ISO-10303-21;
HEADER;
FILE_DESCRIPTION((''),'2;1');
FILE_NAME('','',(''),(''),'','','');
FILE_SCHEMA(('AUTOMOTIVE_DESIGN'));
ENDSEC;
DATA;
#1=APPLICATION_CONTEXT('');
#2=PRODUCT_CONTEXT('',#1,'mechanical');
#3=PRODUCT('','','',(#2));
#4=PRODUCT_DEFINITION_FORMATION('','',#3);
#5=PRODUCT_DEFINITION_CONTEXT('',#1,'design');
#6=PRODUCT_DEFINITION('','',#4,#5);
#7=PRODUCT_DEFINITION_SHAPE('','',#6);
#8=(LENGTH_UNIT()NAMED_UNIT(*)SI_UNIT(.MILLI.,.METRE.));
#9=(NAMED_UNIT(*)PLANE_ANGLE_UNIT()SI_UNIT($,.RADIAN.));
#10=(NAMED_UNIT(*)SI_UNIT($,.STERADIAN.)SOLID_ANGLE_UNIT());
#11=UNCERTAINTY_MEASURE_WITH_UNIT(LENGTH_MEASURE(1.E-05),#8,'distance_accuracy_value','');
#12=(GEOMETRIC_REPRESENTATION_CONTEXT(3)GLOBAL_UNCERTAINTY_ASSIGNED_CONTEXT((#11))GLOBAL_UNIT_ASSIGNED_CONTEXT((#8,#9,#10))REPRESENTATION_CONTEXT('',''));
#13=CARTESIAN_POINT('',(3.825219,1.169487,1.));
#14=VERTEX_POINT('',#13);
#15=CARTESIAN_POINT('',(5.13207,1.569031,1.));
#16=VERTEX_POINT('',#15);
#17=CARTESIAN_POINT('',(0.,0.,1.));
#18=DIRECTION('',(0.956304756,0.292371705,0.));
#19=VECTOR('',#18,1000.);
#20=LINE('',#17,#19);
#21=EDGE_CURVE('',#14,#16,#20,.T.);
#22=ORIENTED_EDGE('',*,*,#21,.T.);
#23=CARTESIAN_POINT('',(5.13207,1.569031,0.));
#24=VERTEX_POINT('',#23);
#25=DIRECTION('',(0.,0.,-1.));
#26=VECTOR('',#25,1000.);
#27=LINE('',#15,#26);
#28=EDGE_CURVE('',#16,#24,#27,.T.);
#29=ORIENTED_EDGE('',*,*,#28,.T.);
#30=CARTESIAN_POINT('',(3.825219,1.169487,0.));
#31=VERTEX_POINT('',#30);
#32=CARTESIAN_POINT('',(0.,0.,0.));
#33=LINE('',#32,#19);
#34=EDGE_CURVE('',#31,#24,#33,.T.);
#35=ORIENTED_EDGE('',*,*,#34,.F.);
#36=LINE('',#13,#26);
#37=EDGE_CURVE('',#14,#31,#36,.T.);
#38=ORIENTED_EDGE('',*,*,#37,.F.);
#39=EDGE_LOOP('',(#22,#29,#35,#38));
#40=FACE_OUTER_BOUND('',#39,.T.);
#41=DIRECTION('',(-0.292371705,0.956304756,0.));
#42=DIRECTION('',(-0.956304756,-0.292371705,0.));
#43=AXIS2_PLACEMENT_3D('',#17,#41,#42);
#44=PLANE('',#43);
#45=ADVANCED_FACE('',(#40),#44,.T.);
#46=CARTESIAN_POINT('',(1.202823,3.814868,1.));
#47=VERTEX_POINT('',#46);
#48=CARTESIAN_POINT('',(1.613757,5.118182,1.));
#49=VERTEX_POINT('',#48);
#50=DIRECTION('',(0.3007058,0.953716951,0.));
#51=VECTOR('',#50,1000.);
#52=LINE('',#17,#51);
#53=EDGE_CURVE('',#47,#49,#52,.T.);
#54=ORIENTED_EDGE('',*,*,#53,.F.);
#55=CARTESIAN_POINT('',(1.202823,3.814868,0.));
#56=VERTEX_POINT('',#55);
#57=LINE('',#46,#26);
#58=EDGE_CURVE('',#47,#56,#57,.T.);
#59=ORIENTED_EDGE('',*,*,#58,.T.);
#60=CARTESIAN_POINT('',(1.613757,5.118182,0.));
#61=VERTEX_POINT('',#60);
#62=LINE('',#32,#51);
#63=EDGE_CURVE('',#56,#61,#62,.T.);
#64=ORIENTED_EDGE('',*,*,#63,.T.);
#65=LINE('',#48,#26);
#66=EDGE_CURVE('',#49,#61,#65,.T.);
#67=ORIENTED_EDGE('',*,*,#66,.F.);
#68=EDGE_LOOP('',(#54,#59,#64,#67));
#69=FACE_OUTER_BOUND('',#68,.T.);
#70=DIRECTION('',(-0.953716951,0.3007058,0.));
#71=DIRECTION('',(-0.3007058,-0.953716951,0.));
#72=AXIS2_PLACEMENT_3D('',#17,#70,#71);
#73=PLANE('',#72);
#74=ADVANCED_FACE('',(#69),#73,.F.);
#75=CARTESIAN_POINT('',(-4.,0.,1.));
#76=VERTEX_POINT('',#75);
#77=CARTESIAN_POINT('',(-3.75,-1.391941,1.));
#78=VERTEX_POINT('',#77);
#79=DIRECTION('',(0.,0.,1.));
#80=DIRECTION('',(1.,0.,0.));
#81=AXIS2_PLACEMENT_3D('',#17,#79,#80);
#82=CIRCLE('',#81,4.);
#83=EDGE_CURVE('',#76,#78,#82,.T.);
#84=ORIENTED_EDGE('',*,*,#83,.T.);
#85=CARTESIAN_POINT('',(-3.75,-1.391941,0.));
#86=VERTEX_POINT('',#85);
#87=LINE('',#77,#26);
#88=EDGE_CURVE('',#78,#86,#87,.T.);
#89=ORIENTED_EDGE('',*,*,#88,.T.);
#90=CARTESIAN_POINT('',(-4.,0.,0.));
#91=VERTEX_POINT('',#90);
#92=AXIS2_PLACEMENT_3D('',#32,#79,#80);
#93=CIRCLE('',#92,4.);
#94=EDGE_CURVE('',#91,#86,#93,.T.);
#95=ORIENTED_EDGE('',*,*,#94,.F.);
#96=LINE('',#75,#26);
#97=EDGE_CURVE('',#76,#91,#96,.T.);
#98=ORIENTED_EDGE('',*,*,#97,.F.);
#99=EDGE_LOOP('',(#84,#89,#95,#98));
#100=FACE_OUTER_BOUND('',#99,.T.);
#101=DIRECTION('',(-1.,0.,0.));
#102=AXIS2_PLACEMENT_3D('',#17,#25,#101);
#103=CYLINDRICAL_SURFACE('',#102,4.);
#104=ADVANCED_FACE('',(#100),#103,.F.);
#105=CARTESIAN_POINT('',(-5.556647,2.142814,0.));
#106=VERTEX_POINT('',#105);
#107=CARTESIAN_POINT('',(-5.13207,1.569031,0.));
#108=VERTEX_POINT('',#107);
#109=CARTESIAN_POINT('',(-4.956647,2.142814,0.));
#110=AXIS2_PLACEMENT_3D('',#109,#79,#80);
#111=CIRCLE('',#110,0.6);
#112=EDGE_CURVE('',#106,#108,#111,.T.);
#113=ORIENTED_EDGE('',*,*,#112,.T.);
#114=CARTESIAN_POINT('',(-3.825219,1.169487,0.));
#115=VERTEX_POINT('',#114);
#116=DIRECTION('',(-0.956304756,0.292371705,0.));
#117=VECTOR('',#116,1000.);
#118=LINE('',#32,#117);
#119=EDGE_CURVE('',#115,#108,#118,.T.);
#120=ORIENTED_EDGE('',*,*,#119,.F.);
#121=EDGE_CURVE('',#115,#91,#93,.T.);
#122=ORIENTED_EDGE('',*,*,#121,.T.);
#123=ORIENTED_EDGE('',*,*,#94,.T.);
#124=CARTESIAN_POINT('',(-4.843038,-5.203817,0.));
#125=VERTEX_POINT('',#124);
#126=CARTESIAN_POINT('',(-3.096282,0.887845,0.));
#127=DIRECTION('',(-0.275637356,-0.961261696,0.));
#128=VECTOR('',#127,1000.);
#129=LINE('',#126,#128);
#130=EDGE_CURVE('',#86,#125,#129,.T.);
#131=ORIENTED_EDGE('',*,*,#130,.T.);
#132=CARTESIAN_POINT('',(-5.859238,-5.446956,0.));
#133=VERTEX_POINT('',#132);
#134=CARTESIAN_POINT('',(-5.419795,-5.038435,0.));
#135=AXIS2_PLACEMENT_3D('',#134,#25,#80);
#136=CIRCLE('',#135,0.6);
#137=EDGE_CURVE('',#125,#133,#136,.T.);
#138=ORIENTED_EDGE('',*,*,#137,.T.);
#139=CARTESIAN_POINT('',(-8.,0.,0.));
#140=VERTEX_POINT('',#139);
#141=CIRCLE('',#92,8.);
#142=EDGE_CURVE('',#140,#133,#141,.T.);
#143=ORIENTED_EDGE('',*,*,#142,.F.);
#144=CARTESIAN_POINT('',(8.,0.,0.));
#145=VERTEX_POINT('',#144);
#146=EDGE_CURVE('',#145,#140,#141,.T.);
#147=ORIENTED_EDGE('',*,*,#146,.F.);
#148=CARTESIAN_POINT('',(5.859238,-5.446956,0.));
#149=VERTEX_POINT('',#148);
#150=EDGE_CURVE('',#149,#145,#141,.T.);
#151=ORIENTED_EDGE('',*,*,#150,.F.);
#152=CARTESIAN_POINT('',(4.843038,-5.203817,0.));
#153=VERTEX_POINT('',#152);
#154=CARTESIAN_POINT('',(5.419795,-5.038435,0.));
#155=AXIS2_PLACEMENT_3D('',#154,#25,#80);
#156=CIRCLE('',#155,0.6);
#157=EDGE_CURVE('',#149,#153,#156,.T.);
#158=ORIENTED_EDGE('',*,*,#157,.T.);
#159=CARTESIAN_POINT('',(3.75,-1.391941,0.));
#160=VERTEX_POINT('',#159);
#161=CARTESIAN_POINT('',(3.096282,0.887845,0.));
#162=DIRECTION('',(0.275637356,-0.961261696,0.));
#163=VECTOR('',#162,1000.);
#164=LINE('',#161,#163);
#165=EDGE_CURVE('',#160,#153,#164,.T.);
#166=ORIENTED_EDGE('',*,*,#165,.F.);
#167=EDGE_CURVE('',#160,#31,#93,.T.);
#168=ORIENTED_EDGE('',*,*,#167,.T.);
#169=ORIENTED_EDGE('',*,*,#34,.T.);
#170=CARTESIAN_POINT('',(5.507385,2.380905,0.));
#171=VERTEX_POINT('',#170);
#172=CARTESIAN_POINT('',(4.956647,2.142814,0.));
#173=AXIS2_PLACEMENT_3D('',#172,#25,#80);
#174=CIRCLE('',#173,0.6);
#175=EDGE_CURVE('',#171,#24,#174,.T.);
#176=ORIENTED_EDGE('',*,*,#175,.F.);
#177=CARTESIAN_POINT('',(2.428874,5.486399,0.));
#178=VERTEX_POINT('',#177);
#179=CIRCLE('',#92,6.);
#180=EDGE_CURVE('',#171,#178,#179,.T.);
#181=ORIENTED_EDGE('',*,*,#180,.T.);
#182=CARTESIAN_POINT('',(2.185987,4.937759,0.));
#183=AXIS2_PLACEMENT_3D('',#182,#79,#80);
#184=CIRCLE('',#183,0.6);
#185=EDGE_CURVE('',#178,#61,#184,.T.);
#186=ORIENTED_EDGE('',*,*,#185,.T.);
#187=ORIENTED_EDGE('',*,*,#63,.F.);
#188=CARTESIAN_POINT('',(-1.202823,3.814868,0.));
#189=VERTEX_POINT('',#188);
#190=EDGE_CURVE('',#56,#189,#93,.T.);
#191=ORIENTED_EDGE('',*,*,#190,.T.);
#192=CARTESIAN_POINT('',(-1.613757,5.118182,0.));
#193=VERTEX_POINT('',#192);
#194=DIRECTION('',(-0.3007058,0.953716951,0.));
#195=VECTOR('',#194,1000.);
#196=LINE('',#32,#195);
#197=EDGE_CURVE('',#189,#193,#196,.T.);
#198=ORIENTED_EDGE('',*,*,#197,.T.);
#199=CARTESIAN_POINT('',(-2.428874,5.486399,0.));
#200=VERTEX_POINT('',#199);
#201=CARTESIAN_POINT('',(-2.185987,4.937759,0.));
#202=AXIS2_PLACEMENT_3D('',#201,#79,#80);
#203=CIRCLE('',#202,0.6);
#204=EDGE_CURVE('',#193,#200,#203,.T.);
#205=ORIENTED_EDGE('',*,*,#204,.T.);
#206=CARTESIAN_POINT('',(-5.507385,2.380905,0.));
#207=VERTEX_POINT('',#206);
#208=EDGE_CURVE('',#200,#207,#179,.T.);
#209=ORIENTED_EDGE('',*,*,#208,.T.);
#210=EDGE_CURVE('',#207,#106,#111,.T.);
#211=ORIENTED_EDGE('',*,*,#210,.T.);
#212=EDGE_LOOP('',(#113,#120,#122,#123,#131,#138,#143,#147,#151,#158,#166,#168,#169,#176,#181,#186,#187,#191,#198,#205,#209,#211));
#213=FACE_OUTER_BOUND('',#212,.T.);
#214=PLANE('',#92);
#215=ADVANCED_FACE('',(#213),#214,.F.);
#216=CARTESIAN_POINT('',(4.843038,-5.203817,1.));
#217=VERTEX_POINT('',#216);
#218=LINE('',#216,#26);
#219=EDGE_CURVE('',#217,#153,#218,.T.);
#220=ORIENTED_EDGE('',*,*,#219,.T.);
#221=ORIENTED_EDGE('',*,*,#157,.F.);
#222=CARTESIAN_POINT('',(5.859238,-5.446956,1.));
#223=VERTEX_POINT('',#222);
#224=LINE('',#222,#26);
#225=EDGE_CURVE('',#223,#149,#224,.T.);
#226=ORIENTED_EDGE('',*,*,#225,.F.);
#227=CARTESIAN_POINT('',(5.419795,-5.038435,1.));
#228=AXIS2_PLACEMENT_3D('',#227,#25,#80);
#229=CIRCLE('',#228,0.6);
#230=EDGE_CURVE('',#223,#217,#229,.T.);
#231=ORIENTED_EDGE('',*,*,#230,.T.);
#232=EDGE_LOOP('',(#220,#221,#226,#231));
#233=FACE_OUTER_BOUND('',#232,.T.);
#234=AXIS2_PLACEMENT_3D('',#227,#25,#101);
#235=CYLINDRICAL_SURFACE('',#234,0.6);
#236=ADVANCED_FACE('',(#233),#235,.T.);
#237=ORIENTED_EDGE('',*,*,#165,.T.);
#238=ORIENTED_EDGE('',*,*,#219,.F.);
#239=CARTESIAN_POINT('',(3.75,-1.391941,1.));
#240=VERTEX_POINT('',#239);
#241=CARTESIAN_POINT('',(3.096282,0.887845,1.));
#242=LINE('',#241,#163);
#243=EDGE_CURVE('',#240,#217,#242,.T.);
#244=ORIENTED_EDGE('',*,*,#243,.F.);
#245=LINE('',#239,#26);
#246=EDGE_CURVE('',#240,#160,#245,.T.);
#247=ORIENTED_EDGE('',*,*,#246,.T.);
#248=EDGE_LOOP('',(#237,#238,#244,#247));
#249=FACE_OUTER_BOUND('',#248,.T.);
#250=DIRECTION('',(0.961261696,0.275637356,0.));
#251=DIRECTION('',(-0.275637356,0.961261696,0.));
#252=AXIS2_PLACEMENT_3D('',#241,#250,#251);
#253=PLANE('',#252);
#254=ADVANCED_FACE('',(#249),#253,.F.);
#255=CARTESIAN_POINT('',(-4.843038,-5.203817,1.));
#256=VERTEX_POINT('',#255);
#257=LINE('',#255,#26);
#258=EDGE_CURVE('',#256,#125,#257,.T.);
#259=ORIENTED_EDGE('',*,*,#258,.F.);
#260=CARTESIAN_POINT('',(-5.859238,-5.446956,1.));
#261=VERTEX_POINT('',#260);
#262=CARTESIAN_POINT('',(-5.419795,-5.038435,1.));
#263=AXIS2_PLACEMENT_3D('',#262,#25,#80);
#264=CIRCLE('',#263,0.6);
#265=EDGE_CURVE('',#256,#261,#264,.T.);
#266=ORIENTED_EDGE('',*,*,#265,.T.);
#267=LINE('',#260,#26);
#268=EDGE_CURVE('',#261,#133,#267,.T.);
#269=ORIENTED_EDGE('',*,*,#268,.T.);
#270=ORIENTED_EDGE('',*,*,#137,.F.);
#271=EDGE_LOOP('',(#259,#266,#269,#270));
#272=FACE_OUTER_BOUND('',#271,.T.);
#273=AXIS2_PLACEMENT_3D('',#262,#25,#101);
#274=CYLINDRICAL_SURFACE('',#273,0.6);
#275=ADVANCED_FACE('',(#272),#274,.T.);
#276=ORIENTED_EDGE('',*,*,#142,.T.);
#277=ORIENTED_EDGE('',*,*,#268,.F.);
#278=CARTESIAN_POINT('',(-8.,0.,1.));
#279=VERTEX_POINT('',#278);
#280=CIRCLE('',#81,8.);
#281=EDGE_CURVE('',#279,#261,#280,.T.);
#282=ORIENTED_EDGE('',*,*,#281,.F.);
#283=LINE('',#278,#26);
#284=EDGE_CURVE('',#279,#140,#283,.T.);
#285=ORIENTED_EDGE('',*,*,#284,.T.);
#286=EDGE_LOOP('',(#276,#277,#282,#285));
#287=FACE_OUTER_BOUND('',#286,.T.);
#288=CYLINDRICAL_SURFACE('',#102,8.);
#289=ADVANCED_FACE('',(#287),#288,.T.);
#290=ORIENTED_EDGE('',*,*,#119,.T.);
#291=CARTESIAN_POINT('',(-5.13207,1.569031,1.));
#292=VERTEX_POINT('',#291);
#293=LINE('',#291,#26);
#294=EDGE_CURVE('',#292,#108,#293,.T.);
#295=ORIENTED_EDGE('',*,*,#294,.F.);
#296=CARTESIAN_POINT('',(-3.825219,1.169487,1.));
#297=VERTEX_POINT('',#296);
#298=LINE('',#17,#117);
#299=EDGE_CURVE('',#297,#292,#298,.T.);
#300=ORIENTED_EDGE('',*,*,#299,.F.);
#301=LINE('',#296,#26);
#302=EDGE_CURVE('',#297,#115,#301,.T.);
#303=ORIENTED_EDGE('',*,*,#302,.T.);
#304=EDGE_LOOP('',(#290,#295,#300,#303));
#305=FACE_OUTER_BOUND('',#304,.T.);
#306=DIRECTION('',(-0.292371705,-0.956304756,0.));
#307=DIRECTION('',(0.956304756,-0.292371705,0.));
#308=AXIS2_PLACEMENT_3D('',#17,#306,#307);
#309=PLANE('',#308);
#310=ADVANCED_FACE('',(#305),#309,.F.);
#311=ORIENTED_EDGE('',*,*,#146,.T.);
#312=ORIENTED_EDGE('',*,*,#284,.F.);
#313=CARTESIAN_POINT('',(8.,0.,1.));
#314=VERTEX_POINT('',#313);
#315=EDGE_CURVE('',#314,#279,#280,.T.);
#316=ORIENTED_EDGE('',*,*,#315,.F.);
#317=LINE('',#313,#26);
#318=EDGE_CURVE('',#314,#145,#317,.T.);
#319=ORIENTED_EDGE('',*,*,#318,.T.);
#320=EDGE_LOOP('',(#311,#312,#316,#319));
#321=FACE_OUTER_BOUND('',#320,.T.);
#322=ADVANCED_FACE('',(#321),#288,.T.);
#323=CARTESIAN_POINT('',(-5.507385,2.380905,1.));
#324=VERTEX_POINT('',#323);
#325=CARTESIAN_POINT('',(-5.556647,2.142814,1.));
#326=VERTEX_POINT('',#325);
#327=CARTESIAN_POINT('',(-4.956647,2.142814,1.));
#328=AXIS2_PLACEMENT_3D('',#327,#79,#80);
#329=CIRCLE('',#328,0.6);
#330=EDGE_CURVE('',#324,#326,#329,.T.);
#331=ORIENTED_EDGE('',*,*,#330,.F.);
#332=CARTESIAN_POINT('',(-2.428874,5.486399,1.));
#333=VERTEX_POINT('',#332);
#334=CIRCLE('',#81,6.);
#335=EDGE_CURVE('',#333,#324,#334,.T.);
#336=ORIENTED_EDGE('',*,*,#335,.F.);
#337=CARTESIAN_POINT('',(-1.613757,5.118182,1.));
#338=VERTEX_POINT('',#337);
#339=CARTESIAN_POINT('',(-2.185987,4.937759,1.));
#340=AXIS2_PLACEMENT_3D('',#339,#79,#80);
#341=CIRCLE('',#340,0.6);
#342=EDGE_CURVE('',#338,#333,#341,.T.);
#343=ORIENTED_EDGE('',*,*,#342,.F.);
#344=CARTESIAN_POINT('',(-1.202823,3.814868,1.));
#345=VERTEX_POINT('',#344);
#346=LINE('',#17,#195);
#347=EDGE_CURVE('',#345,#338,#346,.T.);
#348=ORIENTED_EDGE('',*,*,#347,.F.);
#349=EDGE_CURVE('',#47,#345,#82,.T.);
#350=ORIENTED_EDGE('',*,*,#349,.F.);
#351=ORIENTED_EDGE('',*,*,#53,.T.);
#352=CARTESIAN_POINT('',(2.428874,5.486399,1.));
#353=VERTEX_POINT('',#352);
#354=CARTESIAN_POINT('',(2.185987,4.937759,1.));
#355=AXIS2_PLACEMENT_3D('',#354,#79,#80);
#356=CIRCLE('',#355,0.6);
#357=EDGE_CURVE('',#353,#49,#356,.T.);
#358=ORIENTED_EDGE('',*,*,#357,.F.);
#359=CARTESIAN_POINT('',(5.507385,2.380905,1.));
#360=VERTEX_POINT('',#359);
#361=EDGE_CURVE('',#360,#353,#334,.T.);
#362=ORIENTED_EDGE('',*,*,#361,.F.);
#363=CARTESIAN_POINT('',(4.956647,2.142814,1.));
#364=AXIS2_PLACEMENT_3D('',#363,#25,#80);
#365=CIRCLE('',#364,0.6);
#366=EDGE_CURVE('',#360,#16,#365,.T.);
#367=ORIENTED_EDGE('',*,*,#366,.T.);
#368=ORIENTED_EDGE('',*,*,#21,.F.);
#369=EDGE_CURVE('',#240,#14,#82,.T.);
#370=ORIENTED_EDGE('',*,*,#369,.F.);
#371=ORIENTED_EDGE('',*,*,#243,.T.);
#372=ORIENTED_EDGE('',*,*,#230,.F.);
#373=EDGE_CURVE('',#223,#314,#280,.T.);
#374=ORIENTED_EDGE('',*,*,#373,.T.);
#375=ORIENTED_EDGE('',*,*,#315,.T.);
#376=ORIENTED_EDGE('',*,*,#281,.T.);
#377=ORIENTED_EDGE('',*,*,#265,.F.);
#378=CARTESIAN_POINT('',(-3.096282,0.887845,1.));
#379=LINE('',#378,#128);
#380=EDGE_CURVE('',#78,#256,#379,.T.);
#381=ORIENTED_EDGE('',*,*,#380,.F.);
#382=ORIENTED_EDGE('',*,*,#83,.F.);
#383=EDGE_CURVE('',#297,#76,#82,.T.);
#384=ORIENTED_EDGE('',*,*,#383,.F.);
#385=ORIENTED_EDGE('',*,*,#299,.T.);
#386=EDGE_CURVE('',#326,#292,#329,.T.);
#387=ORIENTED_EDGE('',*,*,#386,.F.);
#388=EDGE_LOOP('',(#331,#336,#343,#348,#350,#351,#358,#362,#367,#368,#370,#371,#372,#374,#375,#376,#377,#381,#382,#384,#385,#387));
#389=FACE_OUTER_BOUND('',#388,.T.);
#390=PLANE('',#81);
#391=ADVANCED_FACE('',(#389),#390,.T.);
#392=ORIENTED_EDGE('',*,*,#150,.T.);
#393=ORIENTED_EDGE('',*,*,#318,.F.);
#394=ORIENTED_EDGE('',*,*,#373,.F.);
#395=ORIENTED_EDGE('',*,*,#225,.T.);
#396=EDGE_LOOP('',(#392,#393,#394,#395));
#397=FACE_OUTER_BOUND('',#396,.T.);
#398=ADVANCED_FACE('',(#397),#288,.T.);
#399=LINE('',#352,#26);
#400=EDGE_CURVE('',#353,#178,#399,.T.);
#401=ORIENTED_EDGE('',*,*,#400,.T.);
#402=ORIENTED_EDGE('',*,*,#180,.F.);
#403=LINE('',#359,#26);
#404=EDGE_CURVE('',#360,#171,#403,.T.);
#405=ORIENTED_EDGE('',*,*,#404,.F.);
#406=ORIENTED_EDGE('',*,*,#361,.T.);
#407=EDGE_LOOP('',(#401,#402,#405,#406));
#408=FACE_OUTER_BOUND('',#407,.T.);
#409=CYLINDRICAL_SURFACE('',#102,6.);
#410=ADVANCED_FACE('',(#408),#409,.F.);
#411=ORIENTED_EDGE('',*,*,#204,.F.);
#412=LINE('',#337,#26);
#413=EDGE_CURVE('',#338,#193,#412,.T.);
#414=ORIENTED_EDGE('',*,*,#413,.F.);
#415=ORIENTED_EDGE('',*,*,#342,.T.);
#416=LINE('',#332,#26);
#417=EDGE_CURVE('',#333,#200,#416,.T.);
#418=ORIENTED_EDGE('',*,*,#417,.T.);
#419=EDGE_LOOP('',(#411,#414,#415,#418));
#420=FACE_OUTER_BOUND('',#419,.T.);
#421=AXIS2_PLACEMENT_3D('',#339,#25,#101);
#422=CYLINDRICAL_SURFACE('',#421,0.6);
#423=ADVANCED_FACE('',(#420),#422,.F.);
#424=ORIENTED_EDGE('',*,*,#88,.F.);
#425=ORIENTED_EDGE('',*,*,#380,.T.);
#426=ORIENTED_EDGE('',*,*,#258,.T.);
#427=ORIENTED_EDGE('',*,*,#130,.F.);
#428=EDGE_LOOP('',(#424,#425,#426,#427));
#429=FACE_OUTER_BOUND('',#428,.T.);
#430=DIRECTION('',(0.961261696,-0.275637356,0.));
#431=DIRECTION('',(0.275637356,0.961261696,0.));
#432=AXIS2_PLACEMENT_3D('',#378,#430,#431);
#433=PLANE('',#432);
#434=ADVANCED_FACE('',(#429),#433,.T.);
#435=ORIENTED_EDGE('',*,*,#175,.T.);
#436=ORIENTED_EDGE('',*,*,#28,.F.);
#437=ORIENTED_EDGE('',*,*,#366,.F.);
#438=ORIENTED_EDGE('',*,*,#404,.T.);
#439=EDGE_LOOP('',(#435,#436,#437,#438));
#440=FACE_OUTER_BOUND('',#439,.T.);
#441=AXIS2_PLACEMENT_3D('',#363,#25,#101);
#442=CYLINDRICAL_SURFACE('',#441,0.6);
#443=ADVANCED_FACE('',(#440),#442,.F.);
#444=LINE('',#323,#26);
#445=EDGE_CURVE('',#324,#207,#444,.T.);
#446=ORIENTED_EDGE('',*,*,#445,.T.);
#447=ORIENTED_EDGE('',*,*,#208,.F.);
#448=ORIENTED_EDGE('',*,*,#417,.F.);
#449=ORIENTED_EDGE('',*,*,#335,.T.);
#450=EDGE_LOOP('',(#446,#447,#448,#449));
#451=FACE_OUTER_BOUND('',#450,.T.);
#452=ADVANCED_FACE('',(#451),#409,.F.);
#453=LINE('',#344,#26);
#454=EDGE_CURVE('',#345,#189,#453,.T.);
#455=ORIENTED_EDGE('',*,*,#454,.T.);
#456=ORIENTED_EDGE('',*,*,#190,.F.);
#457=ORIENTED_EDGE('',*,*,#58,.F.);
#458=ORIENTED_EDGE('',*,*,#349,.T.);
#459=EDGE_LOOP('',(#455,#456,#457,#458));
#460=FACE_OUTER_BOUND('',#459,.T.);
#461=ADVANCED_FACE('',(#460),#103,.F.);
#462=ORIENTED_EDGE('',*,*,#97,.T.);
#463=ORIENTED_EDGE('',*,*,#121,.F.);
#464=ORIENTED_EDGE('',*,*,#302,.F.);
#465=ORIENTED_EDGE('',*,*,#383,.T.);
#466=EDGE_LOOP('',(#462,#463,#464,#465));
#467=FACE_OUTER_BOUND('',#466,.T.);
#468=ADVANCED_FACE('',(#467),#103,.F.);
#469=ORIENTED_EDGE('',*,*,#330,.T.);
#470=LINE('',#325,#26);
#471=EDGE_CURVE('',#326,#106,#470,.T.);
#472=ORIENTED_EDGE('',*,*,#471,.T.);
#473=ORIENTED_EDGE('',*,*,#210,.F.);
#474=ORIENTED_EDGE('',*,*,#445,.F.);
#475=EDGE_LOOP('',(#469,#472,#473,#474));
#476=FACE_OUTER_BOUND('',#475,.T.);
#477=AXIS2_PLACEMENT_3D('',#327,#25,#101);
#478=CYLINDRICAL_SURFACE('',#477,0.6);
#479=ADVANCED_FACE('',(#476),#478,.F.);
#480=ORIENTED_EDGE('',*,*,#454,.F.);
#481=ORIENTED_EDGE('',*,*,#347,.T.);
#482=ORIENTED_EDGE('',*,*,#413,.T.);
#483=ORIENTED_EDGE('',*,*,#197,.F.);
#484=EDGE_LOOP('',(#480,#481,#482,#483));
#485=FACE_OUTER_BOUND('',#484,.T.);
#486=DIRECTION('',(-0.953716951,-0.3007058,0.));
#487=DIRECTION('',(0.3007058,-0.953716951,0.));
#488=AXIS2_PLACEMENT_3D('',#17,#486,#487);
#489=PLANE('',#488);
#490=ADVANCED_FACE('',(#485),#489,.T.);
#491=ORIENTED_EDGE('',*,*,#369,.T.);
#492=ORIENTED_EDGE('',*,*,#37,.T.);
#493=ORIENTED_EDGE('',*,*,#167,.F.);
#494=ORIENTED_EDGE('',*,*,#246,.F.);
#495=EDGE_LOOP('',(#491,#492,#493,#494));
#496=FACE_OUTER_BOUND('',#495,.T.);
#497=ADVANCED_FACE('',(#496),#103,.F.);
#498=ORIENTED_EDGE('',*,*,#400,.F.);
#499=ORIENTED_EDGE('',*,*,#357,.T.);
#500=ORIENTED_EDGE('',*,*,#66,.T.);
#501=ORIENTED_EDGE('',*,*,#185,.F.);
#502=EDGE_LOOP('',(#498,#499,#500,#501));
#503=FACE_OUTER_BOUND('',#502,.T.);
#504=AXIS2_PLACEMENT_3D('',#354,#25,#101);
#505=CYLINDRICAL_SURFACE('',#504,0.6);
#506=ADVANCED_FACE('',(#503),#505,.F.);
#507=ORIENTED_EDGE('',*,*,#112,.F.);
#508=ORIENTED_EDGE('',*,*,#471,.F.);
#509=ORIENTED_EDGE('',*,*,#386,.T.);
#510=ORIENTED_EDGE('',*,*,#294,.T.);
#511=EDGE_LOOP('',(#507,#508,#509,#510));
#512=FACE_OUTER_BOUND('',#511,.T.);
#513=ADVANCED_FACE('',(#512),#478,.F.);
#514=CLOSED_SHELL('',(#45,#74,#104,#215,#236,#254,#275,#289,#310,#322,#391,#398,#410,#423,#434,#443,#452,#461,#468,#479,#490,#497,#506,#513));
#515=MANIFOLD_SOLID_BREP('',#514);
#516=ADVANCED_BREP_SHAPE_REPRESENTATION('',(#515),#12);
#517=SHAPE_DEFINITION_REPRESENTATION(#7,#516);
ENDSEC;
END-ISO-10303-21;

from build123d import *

# Parameters (mm, degrees)
EXTRUDE1_DEPTH = 1


with BuildPart() as part:
    # Sketch1 → Extrude1 (new body)
    with BuildSketch(Plane.XY):
        with BuildLine():
            Line((3.75, -1.391941091), (4.843037844, -5.203817057))
            ThreePointArc((4.843037844, -5.203817057), (5.280177605, -5.621964438), (5.859237689, -5.446956371))
            ThreePointArc((5.859237689, -5.446956371), (0, 8), (-5.859237689, -5.446956371))
            ThreePointArc((-5.859237689, -5.446956371), (-5.280177605, -5.621964438), (-4.843037844, -5.203817057))
            Line((-4.843037844, -5.203817057), (-3.75, -1.391941091))
            ThreePointArc((-3.75, -1.391941091), (-3.998276385, -0.11741359), (-3.825219024, 1.169486819))
            Line((-3.825219024, 1.169486819), (-5.13206986, 1.569031215))
            ThreePointArc((-5.13206986, 1.569031215), (-5.501268007, 1.891044768), (-5.507385374, 2.380904521))
            ThreePointArc((-5.507385374, 2.380904521), (-4.261112254, 4.224088347), (-2.428874258, 5.486398622))
            ThreePointArc((-2.428874258, 5.486398622), (-1.938979773, 5.484556266), (-1.613756661, 5.11818224))
            Line((-1.613756661, 5.11818224), (-1.202823198, 3.814867803))
            ThreePointArc((-1.202823198, 3.814867803), (0, 4), (1.202823198, 3.814867803))
            Line((1.202823198, 3.814867803), (1.613756661, 5.11818224))
            ThreePointArc((1.613756661, 5.11818224), (1.938979773, 5.484556266), (2.428874258, 5.486398622))
            ThreePointArc((2.428874258, 5.486398622), (4.261112254, 4.224088347), (5.507385374, 2.380904521))
            ThreePointArc((5.507385374, 2.380904521), (5.501268007, 1.891044768), (5.13206986, 1.569031215))
            Line((5.13206986, 1.569031215), (3.825219024, 1.169486819))
            ThreePointArc((3.825219024, 1.169486819), (3.998276385, -0.11741359), (3.75, -1.391941091))
        make_face()
    extrude(amount=EXTRUDE1_DEPTH)


solid = part.part
